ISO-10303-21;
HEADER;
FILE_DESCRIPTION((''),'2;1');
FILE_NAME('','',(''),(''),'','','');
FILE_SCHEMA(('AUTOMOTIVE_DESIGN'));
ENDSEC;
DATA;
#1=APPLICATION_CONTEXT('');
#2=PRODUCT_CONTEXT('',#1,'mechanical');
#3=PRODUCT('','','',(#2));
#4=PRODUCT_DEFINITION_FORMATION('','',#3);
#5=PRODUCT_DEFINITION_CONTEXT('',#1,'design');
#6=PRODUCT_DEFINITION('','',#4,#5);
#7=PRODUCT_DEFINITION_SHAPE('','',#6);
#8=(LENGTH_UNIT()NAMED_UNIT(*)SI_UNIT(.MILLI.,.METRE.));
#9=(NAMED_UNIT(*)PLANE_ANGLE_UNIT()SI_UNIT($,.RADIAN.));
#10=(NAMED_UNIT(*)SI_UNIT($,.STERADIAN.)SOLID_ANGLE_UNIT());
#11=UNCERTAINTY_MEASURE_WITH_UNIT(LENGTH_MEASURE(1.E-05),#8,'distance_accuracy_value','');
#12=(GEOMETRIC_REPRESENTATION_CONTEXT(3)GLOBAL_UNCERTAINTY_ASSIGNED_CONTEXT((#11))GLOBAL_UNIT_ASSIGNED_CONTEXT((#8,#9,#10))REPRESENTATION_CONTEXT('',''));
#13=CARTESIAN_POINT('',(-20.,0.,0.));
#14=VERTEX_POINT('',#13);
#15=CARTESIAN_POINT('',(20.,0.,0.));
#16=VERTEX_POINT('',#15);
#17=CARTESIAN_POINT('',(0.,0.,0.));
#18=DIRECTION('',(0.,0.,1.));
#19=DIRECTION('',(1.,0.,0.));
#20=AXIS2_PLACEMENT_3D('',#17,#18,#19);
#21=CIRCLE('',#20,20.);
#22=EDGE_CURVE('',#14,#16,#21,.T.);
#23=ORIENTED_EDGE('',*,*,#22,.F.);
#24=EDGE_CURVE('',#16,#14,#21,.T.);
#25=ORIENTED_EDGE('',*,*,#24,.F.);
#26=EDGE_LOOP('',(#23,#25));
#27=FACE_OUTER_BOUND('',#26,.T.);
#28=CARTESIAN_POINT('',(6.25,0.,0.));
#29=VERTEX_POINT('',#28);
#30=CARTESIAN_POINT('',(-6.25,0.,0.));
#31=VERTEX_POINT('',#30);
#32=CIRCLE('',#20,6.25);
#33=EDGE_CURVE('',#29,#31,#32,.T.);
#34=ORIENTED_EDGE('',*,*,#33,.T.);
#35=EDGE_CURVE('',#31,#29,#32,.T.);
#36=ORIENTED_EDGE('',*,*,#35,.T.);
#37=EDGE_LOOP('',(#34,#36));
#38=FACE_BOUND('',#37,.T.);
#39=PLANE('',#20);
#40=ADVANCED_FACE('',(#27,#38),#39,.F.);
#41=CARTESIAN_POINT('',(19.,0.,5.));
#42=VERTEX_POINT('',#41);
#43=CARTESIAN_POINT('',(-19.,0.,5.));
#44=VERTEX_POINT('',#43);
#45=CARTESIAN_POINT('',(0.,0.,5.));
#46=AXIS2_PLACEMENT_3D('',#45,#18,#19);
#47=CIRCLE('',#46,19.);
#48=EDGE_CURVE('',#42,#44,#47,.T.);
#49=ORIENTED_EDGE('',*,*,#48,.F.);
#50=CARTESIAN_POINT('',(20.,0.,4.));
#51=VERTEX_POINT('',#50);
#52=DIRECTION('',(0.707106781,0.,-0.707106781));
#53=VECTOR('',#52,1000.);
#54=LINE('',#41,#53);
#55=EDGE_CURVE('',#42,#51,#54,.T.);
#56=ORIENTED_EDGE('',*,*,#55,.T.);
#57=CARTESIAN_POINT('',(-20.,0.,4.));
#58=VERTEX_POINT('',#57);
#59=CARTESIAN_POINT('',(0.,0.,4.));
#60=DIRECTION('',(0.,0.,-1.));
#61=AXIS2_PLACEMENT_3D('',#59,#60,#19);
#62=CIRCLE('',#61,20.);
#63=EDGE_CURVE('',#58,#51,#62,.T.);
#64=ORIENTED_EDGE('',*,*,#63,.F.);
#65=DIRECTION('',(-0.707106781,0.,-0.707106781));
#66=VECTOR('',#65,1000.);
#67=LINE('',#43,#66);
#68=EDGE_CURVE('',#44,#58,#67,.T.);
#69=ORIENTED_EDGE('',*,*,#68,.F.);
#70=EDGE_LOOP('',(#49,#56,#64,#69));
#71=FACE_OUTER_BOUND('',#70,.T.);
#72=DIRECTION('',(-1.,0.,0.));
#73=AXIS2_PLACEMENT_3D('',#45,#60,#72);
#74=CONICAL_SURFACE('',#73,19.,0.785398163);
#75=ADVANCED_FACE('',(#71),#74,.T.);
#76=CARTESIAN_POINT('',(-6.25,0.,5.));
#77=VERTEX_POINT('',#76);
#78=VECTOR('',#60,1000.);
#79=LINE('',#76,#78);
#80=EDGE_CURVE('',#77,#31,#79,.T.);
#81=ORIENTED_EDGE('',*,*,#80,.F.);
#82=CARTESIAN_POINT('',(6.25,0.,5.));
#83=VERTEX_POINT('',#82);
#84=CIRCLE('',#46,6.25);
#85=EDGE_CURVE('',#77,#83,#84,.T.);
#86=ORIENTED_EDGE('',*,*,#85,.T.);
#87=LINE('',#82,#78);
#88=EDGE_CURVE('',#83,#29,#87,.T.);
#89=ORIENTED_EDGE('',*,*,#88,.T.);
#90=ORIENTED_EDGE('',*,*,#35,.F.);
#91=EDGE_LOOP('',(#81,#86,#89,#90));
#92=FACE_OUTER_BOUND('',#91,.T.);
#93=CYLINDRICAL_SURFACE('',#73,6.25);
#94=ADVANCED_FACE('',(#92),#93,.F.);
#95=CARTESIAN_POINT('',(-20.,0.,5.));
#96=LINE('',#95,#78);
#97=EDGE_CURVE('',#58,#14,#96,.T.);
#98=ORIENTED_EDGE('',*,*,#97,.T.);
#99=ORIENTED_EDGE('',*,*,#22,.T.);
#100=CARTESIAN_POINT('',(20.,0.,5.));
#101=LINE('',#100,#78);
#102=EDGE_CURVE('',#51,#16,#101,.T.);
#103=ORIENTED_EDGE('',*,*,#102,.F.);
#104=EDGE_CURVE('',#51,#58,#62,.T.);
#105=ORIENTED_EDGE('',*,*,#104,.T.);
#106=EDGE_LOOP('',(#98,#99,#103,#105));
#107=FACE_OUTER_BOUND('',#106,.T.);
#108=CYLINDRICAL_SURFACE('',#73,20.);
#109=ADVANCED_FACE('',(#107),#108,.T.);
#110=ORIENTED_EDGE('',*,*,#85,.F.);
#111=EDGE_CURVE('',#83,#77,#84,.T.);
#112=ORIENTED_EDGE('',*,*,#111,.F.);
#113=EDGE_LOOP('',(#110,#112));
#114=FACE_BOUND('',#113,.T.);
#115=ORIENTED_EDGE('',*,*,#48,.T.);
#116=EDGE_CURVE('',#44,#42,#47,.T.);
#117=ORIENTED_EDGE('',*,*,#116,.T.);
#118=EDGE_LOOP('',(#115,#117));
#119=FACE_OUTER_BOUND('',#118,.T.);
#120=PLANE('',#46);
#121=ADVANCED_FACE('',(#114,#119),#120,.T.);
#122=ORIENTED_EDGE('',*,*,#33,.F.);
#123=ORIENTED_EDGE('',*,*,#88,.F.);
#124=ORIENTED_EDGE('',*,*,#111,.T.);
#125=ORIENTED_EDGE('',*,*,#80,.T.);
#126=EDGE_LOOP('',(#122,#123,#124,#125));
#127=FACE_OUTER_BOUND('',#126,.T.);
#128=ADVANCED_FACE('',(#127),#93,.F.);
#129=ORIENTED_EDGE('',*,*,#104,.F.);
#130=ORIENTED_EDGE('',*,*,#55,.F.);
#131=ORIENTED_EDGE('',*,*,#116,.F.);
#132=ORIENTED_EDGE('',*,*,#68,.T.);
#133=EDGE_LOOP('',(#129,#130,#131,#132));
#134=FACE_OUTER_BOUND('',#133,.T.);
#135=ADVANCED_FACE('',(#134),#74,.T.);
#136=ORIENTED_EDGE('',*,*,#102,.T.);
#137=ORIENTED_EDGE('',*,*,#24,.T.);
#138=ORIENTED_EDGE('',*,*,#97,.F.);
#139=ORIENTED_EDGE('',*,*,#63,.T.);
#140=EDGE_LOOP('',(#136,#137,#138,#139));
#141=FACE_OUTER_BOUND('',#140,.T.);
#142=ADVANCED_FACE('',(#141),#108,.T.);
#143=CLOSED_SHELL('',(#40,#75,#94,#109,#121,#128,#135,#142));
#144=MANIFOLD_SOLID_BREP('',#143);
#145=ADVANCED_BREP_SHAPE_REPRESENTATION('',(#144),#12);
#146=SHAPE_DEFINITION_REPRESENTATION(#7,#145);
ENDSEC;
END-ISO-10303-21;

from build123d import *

# Parameters (mm, degrees)
SKETCH_1_R      = 20
SKETCH_1_R_2    = 6.25
EXTRUDE_1_DEPTH = 5
CHAMFER_1_SIZE  = 1


with BuildPart() as part:
    # 草图1 → 凸台-拉伸1 (new body)
    with BuildSketch(Plane.XY):
        Circle(SKETCH_1_R)
        Circle(SKETCH_1_R_2, mode=Mode.SUBTRACT)
    extrude(amount=EXTRUDE_1_DEPTH)

    # 倒角1
    chamfer_1_edges = [part.edges().sort_by_distance(p)[0] for p in [
        (-20, 0, 5),
    ]]
    chamfer(chamfer_1_edges, length=CHAMFER_1_SIZE)


solid = part.part
